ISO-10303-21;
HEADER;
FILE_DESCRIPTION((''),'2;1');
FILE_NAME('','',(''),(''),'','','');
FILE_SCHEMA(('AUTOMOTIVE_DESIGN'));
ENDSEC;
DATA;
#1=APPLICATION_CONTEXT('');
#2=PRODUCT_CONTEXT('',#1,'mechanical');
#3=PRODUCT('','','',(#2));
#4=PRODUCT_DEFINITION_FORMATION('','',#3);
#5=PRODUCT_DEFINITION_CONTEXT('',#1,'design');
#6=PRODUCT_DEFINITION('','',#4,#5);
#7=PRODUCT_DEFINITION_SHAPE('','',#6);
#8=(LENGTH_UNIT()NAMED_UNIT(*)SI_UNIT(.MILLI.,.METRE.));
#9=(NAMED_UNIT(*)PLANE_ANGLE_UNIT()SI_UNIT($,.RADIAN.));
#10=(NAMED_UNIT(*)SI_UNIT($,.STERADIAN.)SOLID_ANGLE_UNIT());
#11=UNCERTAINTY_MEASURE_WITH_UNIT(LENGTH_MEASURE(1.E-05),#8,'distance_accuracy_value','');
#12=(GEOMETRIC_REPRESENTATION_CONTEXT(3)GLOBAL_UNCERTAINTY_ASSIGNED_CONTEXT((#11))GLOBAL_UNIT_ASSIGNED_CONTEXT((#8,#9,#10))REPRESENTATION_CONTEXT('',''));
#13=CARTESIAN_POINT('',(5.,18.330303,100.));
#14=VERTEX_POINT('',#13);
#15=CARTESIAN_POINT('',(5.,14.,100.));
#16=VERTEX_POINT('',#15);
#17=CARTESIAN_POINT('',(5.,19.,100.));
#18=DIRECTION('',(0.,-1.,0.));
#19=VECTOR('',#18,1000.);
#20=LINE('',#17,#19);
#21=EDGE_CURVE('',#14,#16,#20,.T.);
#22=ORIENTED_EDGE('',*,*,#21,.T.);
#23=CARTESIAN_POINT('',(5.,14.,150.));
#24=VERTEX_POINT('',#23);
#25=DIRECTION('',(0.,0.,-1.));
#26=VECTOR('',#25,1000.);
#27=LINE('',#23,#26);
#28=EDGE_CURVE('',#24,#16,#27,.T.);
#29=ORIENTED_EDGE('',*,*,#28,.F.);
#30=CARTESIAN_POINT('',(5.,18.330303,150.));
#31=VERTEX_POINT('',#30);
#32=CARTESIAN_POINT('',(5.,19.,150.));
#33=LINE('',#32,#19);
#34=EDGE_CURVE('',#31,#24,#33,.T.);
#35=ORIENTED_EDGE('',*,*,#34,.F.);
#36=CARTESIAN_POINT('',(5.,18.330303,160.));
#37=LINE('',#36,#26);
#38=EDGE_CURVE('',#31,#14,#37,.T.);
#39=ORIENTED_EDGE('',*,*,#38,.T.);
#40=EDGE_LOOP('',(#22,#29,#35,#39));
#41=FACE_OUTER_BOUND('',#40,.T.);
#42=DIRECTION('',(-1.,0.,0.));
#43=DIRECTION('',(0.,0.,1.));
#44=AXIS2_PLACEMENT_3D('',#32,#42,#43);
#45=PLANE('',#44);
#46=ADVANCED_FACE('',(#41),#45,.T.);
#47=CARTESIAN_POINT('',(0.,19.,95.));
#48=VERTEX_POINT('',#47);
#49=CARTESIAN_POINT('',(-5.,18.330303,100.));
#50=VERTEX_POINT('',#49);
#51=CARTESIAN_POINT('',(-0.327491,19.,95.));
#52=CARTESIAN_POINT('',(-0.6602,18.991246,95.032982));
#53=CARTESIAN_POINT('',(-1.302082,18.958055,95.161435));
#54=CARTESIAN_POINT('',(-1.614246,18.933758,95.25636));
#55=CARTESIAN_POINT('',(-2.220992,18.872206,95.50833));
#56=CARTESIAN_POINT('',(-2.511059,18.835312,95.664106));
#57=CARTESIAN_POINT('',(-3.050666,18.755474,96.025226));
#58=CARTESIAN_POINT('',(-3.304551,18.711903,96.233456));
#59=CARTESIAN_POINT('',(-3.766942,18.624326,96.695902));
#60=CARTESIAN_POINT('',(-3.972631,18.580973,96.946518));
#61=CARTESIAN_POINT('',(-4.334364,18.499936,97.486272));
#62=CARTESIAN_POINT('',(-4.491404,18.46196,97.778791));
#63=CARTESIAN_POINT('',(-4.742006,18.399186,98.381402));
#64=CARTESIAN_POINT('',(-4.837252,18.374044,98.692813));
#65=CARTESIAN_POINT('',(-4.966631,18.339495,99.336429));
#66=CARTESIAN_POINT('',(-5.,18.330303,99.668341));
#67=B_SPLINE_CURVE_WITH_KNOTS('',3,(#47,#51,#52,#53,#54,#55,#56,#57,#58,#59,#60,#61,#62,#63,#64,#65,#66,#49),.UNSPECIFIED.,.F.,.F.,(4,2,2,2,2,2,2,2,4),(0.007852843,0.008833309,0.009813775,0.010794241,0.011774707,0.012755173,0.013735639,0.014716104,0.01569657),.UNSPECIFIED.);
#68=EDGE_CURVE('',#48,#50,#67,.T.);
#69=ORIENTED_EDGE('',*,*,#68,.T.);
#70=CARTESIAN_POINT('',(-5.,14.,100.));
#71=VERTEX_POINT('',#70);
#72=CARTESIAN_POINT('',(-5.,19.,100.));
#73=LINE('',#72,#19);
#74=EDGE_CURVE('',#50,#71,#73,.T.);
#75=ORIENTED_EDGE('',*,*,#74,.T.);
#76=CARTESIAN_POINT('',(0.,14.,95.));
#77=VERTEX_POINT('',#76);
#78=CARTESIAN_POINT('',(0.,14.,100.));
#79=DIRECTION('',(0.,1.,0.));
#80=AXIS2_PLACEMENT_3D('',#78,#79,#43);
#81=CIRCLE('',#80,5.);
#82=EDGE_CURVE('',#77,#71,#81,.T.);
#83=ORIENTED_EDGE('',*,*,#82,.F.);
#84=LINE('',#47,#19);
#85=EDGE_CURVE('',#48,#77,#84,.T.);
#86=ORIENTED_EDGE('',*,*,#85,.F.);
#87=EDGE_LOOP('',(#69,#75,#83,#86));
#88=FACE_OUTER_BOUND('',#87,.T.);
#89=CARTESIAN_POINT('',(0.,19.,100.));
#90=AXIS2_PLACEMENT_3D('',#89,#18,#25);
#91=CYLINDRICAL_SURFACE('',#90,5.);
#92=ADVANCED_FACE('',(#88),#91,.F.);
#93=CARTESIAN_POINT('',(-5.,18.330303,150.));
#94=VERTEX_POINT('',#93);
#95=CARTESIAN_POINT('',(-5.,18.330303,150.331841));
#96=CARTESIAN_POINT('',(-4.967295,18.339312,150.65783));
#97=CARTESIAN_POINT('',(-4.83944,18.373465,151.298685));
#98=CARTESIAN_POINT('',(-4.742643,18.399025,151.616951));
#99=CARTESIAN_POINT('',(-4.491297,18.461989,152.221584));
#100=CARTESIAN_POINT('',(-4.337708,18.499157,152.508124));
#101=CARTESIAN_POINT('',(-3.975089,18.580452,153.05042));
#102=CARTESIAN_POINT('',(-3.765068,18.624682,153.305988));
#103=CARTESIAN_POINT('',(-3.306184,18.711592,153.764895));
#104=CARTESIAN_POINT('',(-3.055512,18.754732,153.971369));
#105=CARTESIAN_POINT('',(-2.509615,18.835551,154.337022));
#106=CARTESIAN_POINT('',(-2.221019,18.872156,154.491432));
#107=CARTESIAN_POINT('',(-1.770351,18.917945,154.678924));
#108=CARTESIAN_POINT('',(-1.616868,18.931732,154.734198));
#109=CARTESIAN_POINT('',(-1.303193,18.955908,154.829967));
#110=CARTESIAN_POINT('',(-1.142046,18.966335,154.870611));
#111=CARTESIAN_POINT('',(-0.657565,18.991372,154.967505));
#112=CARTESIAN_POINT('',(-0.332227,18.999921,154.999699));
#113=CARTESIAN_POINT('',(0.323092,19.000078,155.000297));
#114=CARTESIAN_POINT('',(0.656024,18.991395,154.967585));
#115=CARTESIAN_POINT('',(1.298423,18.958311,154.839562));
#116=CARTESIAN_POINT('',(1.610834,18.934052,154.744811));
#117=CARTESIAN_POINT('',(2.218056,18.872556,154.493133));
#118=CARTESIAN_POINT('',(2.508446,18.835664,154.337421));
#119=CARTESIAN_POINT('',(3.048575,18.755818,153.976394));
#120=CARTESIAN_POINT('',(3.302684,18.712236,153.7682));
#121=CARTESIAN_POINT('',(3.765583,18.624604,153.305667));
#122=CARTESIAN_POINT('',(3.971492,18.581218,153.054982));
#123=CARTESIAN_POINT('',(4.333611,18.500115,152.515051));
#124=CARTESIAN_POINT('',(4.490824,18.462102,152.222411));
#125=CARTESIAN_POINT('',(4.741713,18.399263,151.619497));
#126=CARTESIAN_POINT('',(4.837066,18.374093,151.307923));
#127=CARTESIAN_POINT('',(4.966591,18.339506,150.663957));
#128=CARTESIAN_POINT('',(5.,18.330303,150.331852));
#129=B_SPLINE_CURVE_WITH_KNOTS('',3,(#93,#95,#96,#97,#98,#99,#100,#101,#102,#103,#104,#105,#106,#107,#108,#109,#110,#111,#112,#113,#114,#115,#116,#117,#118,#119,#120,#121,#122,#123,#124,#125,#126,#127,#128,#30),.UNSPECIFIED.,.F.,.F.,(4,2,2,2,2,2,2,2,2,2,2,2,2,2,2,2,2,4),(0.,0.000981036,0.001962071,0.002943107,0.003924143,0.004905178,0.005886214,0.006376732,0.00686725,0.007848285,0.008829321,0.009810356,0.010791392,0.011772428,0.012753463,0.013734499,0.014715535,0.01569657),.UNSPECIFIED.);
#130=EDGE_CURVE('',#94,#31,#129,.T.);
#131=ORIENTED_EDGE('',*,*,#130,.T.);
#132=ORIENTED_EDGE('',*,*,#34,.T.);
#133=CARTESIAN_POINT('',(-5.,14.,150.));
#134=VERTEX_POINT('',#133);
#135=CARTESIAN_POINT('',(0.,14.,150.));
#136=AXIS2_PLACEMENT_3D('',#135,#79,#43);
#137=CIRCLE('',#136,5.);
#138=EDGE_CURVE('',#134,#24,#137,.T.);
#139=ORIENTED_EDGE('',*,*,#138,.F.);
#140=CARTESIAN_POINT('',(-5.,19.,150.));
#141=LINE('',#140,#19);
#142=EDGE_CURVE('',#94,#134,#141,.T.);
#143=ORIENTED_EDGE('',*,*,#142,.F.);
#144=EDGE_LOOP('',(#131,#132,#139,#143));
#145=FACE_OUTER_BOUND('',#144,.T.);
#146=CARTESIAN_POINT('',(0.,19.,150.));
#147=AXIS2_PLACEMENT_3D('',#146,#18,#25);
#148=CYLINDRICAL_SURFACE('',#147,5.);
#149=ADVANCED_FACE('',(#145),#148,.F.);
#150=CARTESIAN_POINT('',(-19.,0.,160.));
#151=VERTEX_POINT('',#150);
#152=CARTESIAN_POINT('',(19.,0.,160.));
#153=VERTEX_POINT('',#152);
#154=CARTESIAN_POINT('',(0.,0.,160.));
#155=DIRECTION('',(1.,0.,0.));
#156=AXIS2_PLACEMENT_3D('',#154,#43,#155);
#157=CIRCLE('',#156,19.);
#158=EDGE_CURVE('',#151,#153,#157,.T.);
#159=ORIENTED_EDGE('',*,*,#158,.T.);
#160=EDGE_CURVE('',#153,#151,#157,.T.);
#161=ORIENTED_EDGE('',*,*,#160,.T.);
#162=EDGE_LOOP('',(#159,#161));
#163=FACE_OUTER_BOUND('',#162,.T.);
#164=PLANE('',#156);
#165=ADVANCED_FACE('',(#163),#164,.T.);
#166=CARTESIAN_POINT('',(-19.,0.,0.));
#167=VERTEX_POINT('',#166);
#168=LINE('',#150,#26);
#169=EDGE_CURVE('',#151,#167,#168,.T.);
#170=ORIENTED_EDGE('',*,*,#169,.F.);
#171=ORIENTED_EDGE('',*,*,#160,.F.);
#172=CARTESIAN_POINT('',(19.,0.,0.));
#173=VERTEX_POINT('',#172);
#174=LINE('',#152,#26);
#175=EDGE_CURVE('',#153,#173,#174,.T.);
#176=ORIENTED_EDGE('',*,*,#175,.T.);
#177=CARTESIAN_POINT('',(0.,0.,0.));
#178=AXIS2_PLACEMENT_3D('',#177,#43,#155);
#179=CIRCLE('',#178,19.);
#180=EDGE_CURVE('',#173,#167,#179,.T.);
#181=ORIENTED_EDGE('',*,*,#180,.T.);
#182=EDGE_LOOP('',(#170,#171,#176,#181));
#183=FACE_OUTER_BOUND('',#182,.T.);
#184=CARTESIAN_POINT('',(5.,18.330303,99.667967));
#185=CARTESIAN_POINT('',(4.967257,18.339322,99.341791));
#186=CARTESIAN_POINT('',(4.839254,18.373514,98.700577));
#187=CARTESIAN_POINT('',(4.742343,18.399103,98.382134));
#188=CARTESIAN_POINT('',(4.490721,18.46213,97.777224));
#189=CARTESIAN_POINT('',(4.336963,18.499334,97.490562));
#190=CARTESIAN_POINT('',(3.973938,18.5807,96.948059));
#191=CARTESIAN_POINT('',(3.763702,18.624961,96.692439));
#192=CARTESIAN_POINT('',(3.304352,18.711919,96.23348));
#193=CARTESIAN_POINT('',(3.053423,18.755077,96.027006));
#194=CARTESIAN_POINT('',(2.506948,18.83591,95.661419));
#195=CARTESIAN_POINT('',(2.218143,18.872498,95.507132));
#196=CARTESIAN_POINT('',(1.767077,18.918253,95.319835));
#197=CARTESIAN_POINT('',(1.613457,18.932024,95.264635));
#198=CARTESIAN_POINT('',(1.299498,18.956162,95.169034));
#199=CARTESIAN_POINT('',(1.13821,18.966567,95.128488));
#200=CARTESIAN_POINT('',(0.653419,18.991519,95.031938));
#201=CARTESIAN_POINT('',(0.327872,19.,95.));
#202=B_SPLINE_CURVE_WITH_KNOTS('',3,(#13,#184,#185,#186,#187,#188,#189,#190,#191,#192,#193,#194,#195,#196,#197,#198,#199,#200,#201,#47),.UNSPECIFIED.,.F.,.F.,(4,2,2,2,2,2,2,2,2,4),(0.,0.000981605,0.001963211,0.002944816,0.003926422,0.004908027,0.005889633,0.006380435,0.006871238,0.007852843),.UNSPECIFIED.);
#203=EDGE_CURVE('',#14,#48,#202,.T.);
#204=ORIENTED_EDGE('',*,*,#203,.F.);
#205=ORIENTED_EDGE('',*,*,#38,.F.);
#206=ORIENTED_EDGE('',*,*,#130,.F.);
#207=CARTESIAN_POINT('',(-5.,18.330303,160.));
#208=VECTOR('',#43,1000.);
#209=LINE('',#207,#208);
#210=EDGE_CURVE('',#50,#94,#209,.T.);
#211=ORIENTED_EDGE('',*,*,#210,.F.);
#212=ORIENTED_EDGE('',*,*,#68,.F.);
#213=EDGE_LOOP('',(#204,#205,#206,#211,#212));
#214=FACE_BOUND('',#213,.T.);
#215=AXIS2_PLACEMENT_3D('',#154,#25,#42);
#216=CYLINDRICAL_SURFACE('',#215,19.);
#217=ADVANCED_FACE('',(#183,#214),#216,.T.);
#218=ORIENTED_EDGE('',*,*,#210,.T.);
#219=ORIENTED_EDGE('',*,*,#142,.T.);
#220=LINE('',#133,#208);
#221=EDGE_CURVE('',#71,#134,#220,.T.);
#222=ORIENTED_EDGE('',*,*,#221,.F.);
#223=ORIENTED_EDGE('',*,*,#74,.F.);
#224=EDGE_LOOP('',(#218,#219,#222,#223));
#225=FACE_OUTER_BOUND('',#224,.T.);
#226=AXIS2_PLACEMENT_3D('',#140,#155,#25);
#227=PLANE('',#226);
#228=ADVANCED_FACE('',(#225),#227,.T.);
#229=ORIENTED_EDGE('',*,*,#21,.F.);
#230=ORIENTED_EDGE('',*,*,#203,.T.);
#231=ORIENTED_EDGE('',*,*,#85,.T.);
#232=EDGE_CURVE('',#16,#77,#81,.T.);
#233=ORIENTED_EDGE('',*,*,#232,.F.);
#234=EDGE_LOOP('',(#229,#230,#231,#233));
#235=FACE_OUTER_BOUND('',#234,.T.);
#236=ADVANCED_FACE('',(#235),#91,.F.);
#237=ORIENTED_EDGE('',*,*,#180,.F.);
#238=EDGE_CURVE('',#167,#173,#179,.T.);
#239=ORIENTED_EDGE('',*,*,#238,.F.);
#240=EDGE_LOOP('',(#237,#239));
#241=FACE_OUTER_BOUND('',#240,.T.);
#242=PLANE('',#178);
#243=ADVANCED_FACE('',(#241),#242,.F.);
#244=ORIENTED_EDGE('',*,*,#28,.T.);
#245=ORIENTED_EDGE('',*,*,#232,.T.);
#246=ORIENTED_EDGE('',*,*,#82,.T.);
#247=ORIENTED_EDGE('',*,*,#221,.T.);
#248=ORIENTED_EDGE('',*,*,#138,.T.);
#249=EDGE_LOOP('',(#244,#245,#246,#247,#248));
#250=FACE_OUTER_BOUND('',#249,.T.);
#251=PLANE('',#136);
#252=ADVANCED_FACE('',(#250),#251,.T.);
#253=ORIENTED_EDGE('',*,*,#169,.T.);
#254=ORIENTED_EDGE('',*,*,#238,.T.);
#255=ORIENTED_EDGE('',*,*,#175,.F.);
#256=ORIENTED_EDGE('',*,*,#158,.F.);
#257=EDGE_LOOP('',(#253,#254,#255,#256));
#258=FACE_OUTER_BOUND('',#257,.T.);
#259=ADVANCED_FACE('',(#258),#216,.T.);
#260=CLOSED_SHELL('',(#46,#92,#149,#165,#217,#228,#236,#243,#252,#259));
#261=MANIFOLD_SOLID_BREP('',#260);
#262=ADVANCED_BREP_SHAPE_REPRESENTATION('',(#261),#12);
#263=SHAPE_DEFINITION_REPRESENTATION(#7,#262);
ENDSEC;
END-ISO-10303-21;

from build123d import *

# Parameters (mm, degrees)
SKETCH_1_R           = 19
BOSS_EXTRUDE_1_DEPTH = 160
CUT_EXTRUDE_1_DEPTH  = 165.468842034


with BuildPart() as part:
    # Sketch 1 → Boss-Extrude 1 (new body)
    with BuildSketch(Plane.XY):
        Circle(SKETCH_1_R)
    extrude(amount=BOSS_EXTRUDE_1_DEPTH)

    # Sketch 3 → Cut-Extrude 1 (cut, through all)
    with BuildSketch(Plane(origin=(0, 14, 0), x_dir=(1, 0, 0), z_dir=(0, 1, 0))):
        with BuildLine():
            Line((-5, -150), (-5, -100))
            ThreePointArc((-5, -100), (0, -95), (5, -100))
            Line((5, -100), (5, -150))
            ThreePointArc((5, -150), (0, -155), (-5, -150))
        make_face()
    extrude(amount=CUT_EXTRUDE_1_DEPTH, mode=Mode.SUBTRACT)


solid = part.part
